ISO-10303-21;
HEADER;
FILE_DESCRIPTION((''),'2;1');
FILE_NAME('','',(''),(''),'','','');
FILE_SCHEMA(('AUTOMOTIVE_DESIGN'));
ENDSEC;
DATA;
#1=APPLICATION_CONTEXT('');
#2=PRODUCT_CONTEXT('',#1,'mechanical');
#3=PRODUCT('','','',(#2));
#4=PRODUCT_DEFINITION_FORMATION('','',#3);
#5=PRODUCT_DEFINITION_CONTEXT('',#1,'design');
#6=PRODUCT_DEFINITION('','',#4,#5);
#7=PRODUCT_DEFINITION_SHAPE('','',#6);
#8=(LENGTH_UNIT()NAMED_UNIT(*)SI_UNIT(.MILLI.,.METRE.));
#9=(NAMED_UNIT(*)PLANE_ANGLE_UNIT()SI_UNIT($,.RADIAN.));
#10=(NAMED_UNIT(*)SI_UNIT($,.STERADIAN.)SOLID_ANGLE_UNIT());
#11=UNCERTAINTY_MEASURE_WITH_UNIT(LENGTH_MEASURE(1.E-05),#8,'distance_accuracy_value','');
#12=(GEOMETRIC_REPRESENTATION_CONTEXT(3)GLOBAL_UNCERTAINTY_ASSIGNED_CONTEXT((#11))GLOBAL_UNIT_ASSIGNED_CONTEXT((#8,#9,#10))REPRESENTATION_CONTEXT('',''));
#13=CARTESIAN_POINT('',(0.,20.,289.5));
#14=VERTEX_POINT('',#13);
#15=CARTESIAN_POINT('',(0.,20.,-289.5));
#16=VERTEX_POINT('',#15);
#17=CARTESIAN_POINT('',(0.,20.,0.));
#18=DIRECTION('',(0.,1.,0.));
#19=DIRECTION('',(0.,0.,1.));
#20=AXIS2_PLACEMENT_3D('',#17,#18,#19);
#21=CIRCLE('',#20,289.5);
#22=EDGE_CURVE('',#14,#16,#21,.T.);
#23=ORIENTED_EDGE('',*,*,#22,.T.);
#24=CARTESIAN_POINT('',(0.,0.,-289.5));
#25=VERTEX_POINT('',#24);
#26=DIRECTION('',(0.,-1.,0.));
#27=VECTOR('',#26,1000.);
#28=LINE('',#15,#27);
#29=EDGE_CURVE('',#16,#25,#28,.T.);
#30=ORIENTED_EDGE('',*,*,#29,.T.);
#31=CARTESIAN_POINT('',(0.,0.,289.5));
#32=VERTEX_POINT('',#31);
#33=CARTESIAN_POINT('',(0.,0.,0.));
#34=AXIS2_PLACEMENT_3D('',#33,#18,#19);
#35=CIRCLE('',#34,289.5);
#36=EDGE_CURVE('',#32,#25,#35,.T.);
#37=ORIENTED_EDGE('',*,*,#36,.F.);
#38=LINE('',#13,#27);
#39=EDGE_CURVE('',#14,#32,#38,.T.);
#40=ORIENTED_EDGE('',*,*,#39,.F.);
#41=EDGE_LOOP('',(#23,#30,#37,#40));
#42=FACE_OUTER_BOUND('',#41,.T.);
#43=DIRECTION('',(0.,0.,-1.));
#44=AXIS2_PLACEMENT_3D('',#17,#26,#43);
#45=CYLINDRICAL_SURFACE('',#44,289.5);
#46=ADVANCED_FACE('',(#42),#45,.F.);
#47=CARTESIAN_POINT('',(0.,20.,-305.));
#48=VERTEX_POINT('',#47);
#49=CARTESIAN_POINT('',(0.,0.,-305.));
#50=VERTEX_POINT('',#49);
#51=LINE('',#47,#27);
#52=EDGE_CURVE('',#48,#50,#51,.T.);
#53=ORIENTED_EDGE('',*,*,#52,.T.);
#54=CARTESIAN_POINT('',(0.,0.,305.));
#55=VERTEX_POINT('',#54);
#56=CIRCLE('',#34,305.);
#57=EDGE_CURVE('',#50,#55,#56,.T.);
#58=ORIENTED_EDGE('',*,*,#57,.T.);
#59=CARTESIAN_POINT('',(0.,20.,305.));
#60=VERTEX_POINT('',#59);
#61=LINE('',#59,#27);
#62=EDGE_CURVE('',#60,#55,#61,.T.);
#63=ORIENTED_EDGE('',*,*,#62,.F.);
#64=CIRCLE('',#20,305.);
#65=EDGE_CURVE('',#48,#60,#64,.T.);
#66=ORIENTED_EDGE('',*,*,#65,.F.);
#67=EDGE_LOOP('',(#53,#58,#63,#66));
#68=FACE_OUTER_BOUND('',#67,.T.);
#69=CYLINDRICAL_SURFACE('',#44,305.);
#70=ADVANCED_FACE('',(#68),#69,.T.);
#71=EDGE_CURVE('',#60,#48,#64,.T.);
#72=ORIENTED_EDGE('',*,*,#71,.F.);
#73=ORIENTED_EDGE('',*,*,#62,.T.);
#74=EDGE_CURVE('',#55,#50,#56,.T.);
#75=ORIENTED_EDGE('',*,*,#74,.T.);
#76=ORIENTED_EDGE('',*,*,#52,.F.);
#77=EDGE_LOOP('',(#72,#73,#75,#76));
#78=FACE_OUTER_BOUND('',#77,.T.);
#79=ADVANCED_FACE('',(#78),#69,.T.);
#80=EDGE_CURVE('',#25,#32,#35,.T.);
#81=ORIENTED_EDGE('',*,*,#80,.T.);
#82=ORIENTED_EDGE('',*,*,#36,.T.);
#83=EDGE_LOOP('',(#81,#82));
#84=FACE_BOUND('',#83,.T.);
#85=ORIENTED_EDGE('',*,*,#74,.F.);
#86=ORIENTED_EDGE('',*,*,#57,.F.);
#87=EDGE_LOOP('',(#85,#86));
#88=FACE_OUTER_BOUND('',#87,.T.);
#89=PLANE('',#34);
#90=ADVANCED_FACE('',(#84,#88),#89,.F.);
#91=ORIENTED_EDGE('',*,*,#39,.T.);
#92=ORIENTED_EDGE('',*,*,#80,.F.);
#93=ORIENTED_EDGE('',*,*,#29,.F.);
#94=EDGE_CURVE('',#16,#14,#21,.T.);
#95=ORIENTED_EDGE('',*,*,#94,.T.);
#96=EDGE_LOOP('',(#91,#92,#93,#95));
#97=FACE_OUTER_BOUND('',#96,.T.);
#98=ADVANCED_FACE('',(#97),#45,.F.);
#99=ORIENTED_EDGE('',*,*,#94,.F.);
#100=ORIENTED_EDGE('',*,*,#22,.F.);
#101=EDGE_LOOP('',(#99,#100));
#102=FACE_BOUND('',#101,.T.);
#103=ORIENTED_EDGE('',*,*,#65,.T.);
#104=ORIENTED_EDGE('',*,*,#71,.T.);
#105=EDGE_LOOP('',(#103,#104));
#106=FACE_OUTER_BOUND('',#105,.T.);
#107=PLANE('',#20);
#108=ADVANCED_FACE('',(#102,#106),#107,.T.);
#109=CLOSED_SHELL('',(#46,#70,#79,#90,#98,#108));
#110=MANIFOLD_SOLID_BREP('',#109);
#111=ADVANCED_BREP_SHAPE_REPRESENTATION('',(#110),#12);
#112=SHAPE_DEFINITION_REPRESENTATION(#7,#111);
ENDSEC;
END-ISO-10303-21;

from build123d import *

# Parameters (mm, degrees)
SKETCH_1_R      = 305
SKETCH_1_R_2    = 289.5
EXTRUDE_1_DEPTH = 20


with BuildPart() as part:
    # 草图1 → 凸台-拉伸1 (new body)
    with BuildSketch(Plane(origin=(0, 0, 0), x_dir=(1, 0, 0), z_dir=(0, 1, 0))):
        with Locations(Location((0, 0, 0), (0, 0, 270))):
            Circle(SKETCH_1_R)
        with Locations(Location((0, 0, 0), (0, 0, 270))):
            Circle(SKETCH_1_R_2, mode=Mode.SUBTRACT)
    extrude(amount=EXTRUDE_1_DEPTH)


solid = part.part
